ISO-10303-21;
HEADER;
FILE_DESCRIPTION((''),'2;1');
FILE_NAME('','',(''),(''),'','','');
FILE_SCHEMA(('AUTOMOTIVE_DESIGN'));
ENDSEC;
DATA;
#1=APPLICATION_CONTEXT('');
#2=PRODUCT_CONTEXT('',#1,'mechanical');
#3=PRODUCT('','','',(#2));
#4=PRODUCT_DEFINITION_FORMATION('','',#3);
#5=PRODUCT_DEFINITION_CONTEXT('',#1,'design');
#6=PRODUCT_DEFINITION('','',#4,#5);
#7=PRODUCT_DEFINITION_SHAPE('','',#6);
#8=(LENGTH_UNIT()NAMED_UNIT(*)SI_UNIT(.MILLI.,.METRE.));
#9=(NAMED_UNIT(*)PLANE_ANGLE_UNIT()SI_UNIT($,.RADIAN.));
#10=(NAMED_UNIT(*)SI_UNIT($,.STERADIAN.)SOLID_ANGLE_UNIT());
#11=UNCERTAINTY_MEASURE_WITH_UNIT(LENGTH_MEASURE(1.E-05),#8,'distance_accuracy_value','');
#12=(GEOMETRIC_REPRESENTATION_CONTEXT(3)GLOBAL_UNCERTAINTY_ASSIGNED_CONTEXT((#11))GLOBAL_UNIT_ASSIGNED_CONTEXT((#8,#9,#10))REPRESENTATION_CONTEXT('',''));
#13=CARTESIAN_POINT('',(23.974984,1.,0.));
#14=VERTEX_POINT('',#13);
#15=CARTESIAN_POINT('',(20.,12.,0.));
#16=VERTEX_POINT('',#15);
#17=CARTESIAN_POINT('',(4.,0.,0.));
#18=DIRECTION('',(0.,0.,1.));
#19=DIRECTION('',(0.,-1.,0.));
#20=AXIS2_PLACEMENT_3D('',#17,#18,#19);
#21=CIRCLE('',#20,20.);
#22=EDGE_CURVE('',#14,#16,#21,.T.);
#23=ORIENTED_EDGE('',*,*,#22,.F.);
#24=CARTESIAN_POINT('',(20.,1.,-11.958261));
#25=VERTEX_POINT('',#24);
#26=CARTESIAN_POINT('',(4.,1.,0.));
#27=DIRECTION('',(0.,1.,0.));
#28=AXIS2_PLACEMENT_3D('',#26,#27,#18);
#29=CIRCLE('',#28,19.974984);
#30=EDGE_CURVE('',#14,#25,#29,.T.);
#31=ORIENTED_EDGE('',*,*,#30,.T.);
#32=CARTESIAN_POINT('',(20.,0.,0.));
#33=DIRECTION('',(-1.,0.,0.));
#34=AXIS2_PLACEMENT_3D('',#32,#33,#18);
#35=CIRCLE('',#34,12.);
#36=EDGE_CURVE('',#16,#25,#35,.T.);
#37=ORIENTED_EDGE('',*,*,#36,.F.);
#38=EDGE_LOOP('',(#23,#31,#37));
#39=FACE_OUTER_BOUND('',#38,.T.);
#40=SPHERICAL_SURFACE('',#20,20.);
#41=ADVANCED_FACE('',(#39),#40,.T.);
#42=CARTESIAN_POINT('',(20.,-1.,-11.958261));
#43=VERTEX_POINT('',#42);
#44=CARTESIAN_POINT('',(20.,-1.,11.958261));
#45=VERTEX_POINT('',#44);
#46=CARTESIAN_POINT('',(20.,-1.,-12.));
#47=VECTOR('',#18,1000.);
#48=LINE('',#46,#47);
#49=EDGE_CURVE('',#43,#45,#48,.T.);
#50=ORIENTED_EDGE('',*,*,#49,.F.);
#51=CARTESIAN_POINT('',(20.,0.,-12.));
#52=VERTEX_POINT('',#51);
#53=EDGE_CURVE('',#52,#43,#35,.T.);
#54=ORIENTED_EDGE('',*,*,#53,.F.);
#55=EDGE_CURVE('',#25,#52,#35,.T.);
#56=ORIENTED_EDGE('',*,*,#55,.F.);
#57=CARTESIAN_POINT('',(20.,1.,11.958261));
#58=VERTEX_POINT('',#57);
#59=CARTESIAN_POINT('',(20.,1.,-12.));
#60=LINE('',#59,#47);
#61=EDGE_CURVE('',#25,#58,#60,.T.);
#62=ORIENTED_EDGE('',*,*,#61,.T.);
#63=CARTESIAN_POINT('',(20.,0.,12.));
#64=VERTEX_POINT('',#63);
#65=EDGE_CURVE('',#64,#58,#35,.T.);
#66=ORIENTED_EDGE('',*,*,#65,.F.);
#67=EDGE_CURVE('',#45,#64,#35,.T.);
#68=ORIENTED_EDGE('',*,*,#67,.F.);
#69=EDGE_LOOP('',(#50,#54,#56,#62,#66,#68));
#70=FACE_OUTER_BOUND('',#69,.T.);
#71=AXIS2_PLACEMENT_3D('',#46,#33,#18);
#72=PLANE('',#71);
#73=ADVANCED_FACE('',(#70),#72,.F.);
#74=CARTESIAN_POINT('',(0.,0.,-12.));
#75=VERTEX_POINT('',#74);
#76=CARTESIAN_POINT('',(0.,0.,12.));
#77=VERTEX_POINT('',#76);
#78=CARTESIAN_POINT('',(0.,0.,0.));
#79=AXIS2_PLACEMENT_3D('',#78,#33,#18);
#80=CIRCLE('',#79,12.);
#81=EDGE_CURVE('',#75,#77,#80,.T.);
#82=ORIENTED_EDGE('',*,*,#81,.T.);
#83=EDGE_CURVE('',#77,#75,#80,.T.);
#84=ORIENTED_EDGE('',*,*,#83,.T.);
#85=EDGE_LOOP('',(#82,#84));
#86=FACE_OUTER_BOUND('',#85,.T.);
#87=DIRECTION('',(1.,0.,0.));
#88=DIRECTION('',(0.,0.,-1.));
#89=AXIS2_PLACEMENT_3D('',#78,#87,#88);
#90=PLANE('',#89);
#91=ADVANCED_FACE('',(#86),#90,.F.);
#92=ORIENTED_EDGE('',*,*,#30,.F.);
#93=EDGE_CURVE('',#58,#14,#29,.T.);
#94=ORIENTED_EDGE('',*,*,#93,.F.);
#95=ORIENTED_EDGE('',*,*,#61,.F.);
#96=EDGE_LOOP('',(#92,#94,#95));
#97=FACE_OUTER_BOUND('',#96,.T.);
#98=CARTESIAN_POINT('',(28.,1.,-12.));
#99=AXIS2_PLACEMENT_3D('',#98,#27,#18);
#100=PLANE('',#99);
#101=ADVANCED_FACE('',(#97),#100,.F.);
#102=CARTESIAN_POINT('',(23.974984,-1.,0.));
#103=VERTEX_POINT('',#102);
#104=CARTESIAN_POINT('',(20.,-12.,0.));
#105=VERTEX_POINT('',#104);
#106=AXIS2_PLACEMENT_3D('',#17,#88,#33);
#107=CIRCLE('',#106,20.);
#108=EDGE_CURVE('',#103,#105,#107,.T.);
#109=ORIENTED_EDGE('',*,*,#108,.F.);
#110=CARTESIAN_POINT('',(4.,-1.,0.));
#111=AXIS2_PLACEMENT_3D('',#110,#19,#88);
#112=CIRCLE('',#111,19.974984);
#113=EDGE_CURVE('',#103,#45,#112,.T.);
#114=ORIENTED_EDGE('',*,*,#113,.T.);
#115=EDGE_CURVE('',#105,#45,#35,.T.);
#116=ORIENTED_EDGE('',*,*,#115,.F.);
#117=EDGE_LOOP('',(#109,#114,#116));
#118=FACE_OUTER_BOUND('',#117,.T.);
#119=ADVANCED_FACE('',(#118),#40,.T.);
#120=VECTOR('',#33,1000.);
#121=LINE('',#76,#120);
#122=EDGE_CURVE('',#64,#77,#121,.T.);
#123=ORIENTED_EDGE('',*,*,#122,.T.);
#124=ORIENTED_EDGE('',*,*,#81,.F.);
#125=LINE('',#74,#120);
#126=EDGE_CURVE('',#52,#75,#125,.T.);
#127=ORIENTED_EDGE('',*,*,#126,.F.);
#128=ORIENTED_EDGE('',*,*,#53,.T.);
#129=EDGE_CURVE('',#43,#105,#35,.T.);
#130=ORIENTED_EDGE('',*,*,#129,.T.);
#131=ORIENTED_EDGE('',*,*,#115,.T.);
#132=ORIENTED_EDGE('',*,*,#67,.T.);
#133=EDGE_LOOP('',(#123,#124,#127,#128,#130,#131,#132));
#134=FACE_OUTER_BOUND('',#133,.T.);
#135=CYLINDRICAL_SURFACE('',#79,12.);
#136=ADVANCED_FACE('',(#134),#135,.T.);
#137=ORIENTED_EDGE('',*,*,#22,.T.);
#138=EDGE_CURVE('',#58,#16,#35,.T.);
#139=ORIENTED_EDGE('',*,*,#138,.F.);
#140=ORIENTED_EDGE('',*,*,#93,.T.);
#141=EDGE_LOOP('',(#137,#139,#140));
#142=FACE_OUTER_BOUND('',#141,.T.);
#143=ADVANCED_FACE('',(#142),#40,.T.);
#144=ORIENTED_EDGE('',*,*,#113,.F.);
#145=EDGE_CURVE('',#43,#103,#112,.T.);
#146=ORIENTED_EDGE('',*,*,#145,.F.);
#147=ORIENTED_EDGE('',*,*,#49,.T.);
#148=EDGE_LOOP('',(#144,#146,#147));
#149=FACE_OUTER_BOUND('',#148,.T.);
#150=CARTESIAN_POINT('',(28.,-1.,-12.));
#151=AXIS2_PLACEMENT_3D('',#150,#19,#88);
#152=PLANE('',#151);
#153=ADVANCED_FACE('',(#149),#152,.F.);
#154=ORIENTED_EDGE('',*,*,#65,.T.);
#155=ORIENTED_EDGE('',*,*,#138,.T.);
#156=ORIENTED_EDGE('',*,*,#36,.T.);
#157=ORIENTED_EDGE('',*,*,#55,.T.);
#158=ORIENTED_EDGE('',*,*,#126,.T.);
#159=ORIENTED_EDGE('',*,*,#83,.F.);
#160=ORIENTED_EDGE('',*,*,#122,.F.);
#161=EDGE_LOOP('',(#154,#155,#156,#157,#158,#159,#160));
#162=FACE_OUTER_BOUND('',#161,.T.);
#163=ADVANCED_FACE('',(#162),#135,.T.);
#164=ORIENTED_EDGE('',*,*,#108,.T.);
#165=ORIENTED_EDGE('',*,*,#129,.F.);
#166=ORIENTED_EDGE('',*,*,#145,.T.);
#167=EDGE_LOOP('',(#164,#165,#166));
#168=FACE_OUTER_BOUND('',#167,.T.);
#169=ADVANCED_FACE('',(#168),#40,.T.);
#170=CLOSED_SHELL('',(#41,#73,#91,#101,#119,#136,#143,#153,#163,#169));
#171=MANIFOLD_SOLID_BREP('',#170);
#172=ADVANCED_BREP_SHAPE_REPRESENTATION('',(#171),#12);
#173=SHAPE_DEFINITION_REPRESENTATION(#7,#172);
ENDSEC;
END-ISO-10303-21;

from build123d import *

# Parameters (mm, degrees)
CUT_EXTRUDE1_DEPTH      = 30.393876913
CUT_EXTRUDE1_DEPTH_BACK = 30.393876913
SKETCH2_W               = 8
SKETCH2_H               = 2


with BuildPart() as part:
    # Sketch1 → Revolve1 (revolve)
    with BuildSketch(Plane.XY, mode=Mode.PRIVATE) as revolve1_sk:
        with BuildLine():
            Line((0, 0), (0, 12))
            Line((0, 12), (20, 12))
            ThreePointArc((20, 12), (22.973665961, 6.32455532), (24, 0))
            Line((24, 0), (0, 0))
        make_face()
    revolve(revolve1_sk.sketch.rotate(Axis((0, 0, 0), (1, 0, 0)), 90), axis=Axis((0, 0, 0), (1, 0, 0)))

    # Sketch2 → Cut-Extrude1 (cut, two sides: drawn at the far end of the back side and taken through both)
    with BuildSketch(Plane.XY.offset(-CUT_EXTRUDE1_DEPTH_BACK)):
        with Locations((24, 0)):
            Rectangle(SKETCH2_W, SKETCH2_H)
    extrude(amount=CUT_EXTRUDE1_DEPTH + CUT_EXTRUDE1_DEPTH_BACK, mode=Mode.SUBTRACT)


solid = part.part
